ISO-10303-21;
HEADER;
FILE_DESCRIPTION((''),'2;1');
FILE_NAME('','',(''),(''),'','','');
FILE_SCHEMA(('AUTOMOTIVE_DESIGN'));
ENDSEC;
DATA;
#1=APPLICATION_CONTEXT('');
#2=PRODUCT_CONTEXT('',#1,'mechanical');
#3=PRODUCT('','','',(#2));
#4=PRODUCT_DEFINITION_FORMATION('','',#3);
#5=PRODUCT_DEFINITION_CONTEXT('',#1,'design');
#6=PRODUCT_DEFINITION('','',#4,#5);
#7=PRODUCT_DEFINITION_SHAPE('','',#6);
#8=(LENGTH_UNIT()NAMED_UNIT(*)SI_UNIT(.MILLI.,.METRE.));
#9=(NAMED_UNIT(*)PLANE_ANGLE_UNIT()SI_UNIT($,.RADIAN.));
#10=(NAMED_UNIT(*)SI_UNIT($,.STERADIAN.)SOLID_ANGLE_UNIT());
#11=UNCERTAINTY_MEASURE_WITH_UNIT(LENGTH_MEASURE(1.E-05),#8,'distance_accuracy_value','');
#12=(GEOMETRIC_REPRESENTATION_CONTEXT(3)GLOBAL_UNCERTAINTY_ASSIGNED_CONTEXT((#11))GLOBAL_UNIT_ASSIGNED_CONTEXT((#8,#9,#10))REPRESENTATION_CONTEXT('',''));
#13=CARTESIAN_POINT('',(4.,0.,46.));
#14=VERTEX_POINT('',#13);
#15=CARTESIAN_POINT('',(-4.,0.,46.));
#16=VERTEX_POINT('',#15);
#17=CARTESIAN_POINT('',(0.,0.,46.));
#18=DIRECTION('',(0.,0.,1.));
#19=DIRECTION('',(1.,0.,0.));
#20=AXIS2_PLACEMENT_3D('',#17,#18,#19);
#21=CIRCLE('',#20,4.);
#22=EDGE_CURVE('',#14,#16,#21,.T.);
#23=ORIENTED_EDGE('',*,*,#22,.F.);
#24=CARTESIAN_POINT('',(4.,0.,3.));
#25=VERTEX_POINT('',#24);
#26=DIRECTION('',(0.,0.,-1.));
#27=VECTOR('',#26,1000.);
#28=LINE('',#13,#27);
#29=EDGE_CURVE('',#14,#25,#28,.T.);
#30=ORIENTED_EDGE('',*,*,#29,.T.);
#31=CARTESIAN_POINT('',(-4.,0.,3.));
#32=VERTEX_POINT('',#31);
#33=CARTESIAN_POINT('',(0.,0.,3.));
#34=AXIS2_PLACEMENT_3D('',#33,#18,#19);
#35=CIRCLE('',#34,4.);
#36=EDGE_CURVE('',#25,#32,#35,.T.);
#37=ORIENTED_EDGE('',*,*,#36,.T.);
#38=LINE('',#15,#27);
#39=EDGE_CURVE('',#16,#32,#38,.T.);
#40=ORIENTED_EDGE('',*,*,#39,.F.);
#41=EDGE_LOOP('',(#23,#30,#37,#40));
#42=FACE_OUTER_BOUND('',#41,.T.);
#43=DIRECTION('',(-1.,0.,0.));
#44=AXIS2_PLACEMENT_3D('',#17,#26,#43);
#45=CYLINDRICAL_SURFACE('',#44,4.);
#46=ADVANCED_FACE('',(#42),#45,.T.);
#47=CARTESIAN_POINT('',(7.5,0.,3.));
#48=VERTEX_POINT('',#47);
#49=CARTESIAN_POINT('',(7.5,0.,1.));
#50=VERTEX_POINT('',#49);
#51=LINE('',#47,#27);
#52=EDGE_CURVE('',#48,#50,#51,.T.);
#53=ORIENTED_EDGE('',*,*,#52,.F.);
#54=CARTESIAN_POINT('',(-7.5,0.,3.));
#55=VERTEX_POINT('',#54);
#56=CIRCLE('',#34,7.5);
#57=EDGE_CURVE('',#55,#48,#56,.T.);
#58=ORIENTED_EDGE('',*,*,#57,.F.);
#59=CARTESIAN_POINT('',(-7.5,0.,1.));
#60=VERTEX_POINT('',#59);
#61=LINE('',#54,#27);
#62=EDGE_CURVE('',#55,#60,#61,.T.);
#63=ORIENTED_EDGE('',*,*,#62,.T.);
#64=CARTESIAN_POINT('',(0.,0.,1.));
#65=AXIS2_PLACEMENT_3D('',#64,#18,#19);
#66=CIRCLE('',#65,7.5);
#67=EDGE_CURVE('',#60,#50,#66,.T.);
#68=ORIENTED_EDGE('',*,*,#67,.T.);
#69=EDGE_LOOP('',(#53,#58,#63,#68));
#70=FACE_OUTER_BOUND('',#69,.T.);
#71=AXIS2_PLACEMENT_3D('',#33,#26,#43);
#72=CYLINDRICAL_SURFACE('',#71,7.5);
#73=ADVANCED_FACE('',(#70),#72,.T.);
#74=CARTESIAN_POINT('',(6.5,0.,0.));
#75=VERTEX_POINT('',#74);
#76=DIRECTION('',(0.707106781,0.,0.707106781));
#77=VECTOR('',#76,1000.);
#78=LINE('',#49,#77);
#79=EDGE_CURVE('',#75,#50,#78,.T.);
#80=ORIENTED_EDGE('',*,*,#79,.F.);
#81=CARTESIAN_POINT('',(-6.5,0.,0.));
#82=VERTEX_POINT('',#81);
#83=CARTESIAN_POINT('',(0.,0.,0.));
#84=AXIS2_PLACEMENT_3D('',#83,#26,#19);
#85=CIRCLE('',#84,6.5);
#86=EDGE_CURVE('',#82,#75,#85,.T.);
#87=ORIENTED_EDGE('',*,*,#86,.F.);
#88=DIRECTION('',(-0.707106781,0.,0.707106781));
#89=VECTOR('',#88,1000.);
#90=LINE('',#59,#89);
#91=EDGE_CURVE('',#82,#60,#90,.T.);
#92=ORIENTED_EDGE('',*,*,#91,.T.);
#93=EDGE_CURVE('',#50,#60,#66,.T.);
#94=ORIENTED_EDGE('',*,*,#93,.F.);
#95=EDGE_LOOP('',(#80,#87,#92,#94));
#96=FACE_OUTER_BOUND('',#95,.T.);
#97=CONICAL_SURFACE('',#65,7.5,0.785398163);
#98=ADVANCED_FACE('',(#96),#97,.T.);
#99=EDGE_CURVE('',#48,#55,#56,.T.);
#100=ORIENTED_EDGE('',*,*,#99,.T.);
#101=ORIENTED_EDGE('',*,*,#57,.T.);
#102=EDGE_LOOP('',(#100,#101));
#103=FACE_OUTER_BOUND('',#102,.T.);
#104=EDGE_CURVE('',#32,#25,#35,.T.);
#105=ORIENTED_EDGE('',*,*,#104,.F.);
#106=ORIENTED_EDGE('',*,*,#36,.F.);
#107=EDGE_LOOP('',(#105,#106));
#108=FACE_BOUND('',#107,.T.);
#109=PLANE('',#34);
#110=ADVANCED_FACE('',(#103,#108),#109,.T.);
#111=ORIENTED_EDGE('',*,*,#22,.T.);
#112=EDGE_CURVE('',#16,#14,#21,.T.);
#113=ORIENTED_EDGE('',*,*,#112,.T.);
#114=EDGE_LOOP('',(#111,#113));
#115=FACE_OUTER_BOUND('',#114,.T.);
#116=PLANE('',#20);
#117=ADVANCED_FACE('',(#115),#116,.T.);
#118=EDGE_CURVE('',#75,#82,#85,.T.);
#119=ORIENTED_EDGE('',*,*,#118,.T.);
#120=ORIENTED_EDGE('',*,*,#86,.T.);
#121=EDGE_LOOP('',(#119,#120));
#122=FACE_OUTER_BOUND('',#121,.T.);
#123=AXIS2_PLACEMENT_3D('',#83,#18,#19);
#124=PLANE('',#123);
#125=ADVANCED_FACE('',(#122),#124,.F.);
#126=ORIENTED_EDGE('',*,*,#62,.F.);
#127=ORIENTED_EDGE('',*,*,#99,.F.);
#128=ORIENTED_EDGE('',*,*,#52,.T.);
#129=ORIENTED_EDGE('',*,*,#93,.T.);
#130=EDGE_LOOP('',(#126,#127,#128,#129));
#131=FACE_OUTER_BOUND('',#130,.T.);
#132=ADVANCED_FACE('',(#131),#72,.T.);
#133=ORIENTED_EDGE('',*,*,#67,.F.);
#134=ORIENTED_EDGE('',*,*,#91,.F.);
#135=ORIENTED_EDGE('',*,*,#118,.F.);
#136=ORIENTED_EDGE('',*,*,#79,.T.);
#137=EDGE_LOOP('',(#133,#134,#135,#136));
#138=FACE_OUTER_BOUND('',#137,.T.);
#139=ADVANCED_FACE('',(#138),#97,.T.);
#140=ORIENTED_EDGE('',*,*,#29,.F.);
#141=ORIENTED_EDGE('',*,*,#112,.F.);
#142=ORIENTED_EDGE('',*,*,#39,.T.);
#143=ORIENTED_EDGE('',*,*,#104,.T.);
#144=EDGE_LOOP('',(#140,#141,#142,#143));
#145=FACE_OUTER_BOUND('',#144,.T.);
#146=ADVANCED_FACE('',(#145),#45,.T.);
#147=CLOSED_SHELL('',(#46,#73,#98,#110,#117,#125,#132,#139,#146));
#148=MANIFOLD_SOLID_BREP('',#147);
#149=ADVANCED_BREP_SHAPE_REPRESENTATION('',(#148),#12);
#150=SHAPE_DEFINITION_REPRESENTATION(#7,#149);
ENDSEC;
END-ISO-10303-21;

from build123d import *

# Parameters (mm, degrees)
HEAD_PROFILE_15_R      = 7.5
HEAD_15X3_DEPTH        = 3
SHANK_PROFILE_8_R      = 4
SHANK_8X43_DEPTH       = 43
HEAD_CHAMFER_1X45_SIZE = 1


with BuildPart() as part:
    # Head Profile Ø15 → Head Ø15x3 (new body)
    with BuildSketch(Plane.XY):
        Circle(HEAD_PROFILE_15_R)
    extrude(amount=HEAD_15X3_DEPTH)

    # Shank Profile Ø8 → Shank Ø8x43 (add)
    with BuildSketch(Plane.XY.offset(3)):
        Circle(SHANK_PROFILE_8_R)
    extrude(amount=SHANK_8X43_DEPTH)

    # Head Chamfer 1x45°
    head_chamfer_1x45_edges = [part.edges().sort_by_distance(p)[0] for p in [
        (-7.5, 0, 0),
    ]]
    chamfer(head_chamfer_1x45_edges, length=HEAD_CHAMFER_1X45_SIZE)


solid = part.part
